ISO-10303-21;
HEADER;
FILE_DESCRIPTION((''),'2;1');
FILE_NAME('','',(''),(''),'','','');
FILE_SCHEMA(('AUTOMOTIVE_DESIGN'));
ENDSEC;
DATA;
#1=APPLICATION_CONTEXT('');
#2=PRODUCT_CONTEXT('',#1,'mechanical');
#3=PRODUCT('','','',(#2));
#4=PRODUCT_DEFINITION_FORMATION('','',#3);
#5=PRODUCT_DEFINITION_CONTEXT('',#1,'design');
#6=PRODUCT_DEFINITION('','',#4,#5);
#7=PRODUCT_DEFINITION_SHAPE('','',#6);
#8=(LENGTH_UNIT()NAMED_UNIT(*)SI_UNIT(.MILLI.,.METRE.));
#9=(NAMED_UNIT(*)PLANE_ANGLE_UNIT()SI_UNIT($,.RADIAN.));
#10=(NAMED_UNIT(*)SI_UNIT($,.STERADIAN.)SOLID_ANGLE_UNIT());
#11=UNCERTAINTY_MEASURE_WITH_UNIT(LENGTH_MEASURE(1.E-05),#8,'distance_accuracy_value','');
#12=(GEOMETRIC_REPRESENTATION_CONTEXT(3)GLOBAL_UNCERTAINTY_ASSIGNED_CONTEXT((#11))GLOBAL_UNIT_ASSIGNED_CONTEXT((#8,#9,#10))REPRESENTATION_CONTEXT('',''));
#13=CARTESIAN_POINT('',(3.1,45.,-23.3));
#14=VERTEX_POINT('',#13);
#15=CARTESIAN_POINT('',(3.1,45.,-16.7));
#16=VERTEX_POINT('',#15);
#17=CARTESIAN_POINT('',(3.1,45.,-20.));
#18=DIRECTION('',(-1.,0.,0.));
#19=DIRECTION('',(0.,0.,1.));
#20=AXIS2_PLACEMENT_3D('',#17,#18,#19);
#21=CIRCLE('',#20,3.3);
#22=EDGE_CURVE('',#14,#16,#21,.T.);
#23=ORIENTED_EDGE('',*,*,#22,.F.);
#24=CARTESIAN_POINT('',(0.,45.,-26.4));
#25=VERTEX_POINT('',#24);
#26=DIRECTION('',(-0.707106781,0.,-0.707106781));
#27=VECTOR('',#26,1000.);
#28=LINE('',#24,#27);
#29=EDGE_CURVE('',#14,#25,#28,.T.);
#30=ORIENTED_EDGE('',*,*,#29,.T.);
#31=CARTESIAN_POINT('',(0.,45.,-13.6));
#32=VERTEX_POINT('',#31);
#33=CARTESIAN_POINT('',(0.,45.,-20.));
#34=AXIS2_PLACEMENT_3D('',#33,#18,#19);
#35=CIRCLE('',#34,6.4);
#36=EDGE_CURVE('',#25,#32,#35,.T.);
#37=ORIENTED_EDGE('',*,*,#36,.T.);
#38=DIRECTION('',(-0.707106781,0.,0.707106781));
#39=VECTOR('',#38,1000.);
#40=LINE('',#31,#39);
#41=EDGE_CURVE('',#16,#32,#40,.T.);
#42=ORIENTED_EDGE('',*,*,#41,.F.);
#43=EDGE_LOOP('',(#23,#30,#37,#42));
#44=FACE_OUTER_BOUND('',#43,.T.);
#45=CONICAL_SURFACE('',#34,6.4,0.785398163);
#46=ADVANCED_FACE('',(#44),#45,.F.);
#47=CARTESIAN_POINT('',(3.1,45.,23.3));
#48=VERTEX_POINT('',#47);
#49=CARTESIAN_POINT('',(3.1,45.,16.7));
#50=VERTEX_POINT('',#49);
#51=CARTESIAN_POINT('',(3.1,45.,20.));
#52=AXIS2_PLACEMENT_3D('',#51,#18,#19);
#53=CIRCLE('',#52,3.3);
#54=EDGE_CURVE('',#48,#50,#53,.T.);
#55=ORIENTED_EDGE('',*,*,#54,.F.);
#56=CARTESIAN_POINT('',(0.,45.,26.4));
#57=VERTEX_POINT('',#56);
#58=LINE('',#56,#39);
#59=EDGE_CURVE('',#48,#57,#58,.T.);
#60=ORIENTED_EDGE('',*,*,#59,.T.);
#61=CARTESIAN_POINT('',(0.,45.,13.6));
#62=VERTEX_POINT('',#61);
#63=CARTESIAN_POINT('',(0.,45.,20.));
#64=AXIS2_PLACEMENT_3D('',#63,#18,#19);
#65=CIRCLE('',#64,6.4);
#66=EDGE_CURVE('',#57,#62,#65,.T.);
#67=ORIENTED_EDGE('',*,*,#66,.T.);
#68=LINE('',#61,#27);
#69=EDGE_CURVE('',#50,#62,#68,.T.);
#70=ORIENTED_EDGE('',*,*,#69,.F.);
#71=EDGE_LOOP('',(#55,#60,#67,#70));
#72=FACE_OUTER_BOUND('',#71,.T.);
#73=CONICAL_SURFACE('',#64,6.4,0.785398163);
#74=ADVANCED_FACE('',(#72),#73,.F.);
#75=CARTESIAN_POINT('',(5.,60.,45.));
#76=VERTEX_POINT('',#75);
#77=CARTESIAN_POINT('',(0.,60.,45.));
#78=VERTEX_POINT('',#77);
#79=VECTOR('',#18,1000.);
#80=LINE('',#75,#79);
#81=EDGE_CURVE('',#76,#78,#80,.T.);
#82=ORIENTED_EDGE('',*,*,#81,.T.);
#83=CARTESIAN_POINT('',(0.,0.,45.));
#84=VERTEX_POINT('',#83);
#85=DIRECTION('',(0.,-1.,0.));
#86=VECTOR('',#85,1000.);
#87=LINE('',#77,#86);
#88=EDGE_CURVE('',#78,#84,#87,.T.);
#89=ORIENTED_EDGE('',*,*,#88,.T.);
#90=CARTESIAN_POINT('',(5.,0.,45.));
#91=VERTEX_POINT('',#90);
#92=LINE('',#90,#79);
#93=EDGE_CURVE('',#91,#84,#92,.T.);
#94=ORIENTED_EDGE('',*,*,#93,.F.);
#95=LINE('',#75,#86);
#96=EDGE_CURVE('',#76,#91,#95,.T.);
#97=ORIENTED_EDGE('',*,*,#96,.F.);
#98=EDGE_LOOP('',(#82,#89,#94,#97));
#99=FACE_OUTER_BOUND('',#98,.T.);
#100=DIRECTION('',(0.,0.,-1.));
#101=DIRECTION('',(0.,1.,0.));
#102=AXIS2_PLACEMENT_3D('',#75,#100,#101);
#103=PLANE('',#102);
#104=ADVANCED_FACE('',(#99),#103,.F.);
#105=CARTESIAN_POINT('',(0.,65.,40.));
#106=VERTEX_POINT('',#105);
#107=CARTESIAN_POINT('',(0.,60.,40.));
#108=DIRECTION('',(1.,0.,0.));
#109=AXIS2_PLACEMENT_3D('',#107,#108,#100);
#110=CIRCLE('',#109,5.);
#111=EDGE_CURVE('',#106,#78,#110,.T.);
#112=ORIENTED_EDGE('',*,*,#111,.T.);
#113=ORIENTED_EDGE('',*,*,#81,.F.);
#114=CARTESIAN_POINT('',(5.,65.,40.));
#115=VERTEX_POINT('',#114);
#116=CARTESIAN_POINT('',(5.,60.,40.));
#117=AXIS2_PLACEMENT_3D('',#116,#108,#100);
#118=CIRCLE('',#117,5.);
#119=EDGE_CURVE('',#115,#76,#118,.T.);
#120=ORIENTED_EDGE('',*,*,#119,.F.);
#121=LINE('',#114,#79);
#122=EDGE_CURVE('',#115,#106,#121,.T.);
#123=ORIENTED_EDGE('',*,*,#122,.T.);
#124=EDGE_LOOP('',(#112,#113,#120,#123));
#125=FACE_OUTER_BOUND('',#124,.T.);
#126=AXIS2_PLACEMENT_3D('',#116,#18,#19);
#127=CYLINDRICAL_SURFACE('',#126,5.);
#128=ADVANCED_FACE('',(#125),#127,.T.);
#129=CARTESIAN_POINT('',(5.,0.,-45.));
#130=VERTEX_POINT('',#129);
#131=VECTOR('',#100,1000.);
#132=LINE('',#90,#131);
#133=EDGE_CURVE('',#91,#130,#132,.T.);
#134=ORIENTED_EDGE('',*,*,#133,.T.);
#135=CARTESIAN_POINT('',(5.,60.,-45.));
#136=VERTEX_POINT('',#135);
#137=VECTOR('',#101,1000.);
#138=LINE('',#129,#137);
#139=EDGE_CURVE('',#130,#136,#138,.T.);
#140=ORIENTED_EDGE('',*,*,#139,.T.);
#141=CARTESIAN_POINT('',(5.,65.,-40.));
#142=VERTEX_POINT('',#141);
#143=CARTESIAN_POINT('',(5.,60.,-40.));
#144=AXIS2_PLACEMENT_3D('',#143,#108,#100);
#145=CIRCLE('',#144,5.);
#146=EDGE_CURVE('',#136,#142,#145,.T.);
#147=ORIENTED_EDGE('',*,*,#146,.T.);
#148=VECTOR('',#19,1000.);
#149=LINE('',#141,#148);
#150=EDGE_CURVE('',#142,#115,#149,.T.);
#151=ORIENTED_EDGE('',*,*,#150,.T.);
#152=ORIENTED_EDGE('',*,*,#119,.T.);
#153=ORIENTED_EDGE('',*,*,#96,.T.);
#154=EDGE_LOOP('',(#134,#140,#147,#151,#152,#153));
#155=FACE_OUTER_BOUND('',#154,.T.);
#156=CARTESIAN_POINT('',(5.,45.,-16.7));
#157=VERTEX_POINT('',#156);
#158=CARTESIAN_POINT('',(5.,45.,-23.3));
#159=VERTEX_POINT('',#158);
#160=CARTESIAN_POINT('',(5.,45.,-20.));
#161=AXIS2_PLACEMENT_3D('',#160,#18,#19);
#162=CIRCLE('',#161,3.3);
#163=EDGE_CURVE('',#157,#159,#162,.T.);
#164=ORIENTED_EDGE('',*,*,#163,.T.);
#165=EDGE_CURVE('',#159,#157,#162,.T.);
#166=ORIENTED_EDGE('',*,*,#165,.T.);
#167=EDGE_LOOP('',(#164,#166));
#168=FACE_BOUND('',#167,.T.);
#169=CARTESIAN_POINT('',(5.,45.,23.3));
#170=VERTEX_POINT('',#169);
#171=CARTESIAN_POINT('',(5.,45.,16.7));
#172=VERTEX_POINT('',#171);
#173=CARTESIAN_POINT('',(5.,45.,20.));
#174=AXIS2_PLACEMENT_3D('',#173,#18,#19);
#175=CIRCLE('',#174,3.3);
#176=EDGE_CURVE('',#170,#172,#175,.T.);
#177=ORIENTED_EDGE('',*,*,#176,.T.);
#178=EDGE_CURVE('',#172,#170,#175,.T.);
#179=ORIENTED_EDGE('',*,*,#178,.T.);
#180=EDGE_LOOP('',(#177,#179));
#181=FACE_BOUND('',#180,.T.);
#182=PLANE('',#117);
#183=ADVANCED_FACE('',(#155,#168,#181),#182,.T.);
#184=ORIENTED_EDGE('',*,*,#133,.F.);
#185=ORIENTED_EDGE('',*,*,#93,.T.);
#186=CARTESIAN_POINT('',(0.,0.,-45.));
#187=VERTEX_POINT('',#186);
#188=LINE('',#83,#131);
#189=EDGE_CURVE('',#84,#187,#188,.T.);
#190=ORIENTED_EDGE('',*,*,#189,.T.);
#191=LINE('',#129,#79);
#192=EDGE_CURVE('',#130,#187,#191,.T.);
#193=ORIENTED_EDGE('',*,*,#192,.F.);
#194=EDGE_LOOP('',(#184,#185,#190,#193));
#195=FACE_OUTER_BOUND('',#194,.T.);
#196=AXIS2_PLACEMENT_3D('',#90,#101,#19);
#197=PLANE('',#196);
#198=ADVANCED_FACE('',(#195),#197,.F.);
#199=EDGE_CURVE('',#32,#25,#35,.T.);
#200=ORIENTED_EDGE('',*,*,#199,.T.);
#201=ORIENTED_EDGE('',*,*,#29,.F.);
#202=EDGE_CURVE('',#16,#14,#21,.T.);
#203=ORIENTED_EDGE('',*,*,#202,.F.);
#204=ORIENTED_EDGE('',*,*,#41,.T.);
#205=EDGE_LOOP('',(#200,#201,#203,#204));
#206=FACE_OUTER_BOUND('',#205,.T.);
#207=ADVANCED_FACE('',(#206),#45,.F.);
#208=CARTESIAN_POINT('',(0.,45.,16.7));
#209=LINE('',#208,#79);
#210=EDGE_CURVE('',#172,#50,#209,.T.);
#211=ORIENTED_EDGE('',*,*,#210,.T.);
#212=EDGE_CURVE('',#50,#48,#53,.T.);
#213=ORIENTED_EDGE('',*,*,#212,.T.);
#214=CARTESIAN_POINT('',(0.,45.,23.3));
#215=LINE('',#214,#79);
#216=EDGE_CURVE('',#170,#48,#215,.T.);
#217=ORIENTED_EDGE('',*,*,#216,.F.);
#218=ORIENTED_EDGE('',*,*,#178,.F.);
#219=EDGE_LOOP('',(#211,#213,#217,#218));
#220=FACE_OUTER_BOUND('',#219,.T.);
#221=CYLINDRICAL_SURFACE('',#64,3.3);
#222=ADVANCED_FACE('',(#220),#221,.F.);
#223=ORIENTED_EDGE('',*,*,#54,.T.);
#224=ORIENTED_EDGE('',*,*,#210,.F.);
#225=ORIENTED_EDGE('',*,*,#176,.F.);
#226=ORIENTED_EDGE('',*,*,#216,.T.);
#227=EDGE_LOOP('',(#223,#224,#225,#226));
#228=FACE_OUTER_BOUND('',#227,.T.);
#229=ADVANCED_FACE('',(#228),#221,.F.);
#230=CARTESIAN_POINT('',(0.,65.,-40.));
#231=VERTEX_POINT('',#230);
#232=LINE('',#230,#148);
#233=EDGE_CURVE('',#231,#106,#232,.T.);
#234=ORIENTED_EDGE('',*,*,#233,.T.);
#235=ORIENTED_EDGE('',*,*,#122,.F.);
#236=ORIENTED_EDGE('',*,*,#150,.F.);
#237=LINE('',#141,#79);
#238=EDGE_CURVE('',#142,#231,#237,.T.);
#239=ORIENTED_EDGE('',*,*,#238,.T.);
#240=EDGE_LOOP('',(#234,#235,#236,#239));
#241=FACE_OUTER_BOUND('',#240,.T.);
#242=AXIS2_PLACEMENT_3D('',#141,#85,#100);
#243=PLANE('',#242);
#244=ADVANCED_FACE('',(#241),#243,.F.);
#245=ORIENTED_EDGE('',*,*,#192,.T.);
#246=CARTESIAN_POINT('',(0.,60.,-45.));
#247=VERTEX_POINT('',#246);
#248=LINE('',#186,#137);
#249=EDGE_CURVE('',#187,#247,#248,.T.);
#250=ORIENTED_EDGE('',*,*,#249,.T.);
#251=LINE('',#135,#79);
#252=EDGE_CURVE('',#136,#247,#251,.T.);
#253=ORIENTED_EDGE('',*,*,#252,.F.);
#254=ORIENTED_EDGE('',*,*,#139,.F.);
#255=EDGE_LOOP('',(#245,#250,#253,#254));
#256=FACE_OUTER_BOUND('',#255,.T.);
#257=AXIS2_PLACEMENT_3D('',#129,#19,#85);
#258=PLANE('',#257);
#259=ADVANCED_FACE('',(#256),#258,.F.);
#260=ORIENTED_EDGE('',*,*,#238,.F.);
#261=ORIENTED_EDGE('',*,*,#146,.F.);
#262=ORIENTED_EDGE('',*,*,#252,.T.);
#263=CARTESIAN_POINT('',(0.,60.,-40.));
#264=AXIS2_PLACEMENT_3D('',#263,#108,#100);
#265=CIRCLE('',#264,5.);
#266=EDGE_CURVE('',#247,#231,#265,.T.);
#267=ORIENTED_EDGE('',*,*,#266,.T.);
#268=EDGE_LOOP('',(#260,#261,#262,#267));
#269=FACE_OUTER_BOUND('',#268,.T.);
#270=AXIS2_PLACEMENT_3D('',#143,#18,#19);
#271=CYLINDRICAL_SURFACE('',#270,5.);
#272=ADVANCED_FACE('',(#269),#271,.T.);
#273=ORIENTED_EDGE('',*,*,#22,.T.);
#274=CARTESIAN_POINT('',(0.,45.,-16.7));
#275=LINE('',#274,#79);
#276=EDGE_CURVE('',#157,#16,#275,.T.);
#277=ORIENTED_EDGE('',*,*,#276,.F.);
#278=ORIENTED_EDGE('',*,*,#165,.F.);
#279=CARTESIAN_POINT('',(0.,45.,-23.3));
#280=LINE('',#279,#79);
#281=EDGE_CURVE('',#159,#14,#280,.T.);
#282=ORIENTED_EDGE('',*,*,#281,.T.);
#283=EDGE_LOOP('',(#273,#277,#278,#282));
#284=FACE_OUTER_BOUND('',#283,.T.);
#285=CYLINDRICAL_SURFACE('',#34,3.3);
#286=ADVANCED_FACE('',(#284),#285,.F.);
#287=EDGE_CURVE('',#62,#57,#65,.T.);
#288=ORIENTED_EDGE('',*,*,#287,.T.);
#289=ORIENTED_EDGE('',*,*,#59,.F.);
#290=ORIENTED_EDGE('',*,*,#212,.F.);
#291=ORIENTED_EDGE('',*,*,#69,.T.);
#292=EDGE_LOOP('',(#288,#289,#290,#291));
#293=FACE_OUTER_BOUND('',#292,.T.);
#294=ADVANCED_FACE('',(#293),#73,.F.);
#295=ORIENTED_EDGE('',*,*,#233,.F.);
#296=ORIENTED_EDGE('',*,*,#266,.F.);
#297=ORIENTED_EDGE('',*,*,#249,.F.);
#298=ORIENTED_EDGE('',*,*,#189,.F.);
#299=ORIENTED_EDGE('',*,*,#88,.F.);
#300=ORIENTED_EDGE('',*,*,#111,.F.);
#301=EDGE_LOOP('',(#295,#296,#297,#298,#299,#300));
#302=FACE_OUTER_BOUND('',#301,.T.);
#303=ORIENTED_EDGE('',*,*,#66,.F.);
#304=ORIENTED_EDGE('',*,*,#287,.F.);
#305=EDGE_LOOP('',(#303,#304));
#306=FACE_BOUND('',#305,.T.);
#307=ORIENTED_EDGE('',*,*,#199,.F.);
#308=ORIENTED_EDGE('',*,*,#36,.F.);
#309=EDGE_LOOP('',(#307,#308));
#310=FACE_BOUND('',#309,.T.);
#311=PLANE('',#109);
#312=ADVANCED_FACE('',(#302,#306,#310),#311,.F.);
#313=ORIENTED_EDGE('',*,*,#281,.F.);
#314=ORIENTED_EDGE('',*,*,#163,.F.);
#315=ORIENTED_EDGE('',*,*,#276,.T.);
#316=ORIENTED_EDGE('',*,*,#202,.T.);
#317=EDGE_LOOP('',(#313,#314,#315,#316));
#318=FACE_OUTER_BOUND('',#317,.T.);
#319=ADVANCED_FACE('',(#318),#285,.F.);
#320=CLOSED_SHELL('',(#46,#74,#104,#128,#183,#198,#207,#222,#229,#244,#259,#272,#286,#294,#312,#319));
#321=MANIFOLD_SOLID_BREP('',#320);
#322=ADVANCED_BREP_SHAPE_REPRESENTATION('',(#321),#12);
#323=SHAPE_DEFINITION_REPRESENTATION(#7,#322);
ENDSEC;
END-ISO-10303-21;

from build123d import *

# Parameters (mm, degrees)
BOSS_EXTRUDE1_DEPTH                         = 5
HOLE_SIZE_BY_HEX_SOCKET_COUNTERSUNK_2_COUNT = 2
HOLE_SIZE_BY_HEX_SOCKET_COUNTERSUNK_2_PITCH = 40


with BuildPart() as part:
    # Sketch1 → Boss-Extrude1 (new body)
    with BuildSketch(Plane(origin=(0, 0, 0), x_dir=(0, 0, -1), z_dir=(1, 0, 0))):
        with BuildLine():
            Line((-45, 60), (-45, 0))
            Line((-45, 0), (45, 0))
            Line((45, 0), (45, 60))
            ThreePointArc((45, 60), (43.535533906, 63.535533906), (40, 65))
            Line((40, 65), (-40, 65))
            ThreePointArc((-40, 65), (-43.535533906, 63.535533906), (-45, 60))
        make_face()
    extrude(amount=BOSS_EXTRUDE1_DEPTH)

    # Sketch2 → Hole size by hex socket countersunk screw type1 (revolve, cut)
    with BuildSketch(Plane(origin=(0, 45, -20), x_dir=(0, 0, 1), z_dir=(0, 1, 0))):
        Polygon((0, 0), (0, 5), (3.3, 5), (3.3, 3.1), (6.4, 0), align=None)
    hole_size_by_hex_socket_countersunk_scre = revolve(axis=Axis((-6.35, 45, -20), (1, 0, 0)), mode=Mode.SUBTRACT)

    # Hole size by hex socket countersunk  2: Hole size by hex socket countersunk screw type1 ×2
    with Locations(*[(0, 0, i * HOLE_SIZE_BY_HEX_SOCKET_COUNTERSUNK_2_PITCH) for i in range(1, HOLE_SIZE_BY_HEX_SOCKET_COUNTERSUNK_2_COUNT)]):
        add(hole_size_by_hex_socket_countersunk_scre, mode=Mode.SUBTRACT)


solid = part.part
